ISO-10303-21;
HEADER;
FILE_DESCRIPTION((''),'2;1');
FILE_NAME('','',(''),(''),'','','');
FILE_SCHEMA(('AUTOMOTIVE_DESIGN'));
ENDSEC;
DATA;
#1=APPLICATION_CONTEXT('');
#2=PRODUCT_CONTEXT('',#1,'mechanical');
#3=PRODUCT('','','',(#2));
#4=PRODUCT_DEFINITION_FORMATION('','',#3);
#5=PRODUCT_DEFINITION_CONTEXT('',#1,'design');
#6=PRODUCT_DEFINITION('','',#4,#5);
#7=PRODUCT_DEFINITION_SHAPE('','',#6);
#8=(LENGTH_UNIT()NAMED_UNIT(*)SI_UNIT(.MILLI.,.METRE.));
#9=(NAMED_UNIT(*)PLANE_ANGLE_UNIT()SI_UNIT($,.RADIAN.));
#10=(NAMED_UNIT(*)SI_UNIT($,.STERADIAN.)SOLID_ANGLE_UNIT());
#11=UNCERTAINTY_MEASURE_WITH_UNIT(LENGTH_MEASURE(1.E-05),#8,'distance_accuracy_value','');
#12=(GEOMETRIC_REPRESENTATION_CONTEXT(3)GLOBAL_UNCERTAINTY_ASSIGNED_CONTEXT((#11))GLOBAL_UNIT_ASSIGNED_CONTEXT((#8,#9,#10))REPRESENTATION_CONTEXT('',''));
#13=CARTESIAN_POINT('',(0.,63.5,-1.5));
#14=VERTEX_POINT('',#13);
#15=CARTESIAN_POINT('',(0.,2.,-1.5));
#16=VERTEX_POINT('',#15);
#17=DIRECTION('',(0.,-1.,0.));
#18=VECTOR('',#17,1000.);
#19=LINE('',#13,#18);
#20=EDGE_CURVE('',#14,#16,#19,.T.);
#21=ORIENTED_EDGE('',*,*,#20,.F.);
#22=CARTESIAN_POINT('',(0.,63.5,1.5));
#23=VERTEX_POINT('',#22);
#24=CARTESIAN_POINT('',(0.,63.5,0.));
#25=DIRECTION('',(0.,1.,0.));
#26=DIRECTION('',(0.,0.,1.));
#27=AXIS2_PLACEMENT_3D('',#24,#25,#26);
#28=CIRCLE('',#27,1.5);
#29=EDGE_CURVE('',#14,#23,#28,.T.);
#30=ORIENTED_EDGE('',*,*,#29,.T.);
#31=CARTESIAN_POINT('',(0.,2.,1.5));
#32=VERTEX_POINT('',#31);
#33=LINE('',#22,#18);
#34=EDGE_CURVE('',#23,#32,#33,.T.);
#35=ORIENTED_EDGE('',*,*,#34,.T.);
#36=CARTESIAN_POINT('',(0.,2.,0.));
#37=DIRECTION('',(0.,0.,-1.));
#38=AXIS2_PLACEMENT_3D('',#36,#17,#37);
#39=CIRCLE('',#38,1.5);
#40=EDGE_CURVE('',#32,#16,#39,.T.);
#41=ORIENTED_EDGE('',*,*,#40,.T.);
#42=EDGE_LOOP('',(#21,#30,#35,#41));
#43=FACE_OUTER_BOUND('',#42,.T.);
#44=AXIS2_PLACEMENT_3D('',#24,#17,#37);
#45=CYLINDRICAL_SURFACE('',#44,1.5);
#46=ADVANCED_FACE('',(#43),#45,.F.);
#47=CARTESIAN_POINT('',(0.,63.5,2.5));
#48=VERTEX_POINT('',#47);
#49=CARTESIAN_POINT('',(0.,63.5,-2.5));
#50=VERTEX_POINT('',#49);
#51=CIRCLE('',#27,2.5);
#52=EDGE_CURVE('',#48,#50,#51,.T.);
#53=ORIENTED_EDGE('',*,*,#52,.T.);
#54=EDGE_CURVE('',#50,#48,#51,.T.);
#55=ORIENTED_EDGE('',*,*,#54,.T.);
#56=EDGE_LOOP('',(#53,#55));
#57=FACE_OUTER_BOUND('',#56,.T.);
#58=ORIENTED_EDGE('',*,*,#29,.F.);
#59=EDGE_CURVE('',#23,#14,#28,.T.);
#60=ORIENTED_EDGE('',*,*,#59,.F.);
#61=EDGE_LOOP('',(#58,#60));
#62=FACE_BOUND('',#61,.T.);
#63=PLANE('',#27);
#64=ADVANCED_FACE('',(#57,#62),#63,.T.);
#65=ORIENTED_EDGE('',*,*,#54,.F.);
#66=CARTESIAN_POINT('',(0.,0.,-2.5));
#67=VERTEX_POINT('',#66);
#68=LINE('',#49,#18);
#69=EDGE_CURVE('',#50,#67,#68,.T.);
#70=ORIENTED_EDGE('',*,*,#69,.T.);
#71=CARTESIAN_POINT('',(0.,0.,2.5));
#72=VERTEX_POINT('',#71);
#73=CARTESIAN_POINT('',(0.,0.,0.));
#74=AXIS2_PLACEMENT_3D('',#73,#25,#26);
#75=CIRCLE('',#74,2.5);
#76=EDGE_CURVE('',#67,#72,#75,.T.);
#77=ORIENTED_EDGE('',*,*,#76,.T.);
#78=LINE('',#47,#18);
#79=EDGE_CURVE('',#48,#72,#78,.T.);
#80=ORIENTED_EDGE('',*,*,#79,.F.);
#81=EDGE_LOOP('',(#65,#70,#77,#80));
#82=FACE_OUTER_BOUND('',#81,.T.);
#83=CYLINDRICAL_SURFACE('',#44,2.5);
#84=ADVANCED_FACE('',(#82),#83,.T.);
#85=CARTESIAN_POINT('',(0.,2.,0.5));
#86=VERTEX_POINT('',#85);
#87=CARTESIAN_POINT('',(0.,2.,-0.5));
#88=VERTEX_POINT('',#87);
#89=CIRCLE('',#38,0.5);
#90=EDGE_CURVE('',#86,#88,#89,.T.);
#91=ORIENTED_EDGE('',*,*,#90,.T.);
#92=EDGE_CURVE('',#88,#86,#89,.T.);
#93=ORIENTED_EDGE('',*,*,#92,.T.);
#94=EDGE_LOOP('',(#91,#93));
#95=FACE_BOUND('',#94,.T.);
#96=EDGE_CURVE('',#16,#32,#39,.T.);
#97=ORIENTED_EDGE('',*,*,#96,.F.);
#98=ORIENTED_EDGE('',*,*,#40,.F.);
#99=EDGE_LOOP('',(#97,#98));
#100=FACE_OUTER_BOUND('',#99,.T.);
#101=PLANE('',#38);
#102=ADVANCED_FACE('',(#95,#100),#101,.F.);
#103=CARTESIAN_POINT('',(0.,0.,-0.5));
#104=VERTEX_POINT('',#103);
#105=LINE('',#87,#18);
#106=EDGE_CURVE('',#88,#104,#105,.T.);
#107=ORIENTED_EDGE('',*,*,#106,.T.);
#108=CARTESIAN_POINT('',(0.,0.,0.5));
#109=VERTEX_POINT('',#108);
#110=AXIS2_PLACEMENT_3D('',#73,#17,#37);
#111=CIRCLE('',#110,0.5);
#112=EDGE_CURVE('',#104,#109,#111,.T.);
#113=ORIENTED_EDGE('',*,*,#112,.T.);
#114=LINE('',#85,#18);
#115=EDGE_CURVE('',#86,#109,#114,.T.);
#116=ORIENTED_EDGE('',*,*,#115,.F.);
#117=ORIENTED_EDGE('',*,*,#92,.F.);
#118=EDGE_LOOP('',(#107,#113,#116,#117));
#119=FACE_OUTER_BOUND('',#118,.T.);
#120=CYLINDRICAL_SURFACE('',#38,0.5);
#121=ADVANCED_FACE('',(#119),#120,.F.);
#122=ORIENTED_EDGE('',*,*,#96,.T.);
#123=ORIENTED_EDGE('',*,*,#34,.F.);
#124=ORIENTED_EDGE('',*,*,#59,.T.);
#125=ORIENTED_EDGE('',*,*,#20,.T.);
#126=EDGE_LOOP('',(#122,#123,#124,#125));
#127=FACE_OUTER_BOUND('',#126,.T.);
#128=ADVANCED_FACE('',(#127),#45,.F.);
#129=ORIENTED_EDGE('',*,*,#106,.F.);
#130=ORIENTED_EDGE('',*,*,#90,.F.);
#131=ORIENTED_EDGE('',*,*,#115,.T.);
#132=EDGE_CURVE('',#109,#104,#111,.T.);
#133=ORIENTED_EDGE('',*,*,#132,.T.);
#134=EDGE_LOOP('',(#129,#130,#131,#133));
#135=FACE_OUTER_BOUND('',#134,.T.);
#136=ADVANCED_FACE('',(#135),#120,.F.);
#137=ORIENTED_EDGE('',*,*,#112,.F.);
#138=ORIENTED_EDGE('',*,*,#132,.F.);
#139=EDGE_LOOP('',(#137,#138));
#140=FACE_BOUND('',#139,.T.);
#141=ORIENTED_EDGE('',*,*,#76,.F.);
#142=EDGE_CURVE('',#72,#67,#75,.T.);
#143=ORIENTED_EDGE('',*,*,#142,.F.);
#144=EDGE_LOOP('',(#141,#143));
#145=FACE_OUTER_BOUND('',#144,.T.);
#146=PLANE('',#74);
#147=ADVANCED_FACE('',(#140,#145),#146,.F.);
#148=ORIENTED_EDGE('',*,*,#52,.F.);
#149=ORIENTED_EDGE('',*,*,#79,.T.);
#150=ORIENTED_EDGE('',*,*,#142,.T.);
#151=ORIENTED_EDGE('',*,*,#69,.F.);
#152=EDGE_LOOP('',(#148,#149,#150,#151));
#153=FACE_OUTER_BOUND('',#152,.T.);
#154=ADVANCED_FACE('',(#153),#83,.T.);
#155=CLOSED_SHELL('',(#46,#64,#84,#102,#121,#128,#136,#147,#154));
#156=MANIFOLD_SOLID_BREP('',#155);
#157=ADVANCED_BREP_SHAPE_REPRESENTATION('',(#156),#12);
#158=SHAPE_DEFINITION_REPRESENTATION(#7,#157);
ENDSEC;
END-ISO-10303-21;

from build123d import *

# Parameters (mm, degrees)
SKETCH1_R           = 2.5
SKETCH1_R_2         = 1.5
BOSS_EXTRUDE1_DEPTH = 63.5
SKETCH2_R           = 1.5
SKETCH2_R_2         = 0.5
BOSS_EXTRUDE2_DEPTH = 2


with BuildPart() as part:
    # Sketch1 → Boss-Extrude1 (new body)
    with BuildSketch(Plane(origin=(0, 0, 0), x_dir=(1, 0, 0), z_dir=(0, 1, 0))):
        with Locations(Location((0, 0, 0), (0, 0, 270))):
            Circle(SKETCH1_R)
        with Locations(Location((0, 0, 0), (0, 0, 270))):
            Circle(SKETCH1_R_2, mode=Mode.SUBTRACT)
    extrude(amount=BOSS_EXTRUDE1_DEPTH)

    # Sketch2 → Boss-Extrude2 (add)
    with BuildSketch(Plane.XZ):
        with Locations(Location((0, 0, 0), (0, 0, 270))):
            Circle(SKETCH2_R)
        with Locations(Location((0, 0, 0), (0, 0, 270))):
            Circle(SKETCH2_R_2, mode=Mode.SUBTRACT)
    extrude(amount=-BOSS_EXTRUDE2_DEPTH)


solid = part.part
